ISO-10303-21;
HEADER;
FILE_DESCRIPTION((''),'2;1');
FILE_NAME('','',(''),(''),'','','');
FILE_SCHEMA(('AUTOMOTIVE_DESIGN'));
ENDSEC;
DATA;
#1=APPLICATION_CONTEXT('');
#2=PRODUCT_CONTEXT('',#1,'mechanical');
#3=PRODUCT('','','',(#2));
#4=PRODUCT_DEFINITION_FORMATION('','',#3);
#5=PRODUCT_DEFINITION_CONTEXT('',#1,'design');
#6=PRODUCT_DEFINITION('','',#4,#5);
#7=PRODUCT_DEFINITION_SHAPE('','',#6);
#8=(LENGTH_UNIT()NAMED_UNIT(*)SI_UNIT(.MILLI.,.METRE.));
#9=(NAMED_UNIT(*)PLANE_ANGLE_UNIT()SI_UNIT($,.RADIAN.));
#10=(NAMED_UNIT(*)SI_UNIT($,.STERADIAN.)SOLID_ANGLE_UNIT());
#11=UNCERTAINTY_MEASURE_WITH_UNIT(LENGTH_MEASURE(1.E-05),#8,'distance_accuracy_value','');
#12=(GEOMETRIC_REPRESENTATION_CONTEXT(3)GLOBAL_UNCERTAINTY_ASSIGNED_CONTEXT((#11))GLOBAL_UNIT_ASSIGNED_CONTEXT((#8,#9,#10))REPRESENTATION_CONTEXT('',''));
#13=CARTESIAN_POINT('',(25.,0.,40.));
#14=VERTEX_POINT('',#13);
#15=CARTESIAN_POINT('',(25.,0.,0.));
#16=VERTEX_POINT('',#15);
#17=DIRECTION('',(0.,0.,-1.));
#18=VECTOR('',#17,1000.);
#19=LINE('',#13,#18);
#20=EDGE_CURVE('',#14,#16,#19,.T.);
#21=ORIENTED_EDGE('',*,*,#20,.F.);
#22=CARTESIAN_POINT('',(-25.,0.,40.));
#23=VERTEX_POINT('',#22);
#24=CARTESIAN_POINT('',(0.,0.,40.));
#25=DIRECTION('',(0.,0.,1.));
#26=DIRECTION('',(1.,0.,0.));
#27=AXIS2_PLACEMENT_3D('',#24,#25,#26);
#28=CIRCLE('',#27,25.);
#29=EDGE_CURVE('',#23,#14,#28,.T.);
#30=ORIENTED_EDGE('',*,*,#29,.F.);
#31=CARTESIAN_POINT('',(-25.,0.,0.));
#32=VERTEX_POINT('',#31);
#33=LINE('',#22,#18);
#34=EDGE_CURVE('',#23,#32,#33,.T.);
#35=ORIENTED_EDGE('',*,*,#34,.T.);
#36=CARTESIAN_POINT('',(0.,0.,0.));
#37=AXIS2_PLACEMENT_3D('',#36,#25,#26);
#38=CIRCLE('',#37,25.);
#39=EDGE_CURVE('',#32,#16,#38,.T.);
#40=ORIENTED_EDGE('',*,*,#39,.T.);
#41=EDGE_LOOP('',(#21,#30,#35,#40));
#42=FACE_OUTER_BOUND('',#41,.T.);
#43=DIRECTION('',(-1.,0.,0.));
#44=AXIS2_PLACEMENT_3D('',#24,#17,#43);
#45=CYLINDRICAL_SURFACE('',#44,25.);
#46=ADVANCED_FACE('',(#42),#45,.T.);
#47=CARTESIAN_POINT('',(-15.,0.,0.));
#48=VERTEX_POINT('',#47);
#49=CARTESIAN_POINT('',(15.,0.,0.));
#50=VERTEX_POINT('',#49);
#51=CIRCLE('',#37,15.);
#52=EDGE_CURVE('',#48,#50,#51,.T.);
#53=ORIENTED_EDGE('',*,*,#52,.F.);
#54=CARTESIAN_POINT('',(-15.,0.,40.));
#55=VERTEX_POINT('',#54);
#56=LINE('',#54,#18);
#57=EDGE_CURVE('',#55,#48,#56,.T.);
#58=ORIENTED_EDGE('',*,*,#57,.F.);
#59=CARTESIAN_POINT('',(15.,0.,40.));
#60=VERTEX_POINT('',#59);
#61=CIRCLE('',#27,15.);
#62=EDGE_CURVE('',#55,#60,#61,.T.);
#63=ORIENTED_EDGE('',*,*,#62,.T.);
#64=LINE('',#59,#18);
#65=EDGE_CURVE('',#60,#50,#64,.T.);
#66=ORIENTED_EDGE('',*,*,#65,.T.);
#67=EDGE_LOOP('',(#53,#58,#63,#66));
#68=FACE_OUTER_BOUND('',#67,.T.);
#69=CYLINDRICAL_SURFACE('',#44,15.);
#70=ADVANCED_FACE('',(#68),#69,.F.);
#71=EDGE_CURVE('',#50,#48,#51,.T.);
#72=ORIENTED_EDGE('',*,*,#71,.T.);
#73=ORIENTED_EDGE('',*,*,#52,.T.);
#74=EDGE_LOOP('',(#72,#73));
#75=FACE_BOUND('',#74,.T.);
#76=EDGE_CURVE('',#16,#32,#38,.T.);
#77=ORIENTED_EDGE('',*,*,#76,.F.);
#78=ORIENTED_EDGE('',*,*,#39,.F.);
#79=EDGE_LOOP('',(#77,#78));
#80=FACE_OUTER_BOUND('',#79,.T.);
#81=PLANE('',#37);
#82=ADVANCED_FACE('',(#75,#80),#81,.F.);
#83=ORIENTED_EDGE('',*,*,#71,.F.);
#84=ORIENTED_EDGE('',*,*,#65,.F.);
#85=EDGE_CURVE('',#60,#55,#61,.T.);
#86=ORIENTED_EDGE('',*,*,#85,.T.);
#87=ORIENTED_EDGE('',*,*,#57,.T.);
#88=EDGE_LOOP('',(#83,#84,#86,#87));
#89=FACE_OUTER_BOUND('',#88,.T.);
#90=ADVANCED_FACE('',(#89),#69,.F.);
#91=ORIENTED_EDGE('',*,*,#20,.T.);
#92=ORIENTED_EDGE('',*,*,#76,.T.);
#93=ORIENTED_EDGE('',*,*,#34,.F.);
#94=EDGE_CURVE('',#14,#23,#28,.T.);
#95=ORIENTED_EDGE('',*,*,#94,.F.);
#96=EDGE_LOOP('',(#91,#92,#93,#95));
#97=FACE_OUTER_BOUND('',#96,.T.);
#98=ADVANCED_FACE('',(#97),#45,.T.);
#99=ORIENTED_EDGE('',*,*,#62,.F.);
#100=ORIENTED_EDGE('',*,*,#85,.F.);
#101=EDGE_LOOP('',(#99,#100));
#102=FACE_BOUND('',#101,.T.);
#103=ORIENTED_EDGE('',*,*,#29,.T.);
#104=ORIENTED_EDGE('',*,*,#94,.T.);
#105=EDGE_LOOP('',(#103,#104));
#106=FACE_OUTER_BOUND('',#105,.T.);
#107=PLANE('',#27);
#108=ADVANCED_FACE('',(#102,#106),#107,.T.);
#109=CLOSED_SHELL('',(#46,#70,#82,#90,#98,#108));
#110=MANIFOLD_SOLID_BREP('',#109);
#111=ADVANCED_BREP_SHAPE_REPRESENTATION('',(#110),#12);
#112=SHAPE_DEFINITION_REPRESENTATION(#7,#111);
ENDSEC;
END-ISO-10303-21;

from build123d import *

# Parameters (mm, degrees)
SKETCH1_R           = 25
SKETCH1_R_2         = 15
BOSS_EXTRUDE1_DEPTH = 40


with BuildPart() as part:
    # Sketch1 → Boss-Extrude1 (new body)
    with BuildSketch(Plane.XY):
        Circle(SKETCH1_R)
        Circle(SKETCH1_R_2, mode=Mode.SUBTRACT)
    extrude(amount=BOSS_EXTRUDE1_DEPTH)


solid = part.part
